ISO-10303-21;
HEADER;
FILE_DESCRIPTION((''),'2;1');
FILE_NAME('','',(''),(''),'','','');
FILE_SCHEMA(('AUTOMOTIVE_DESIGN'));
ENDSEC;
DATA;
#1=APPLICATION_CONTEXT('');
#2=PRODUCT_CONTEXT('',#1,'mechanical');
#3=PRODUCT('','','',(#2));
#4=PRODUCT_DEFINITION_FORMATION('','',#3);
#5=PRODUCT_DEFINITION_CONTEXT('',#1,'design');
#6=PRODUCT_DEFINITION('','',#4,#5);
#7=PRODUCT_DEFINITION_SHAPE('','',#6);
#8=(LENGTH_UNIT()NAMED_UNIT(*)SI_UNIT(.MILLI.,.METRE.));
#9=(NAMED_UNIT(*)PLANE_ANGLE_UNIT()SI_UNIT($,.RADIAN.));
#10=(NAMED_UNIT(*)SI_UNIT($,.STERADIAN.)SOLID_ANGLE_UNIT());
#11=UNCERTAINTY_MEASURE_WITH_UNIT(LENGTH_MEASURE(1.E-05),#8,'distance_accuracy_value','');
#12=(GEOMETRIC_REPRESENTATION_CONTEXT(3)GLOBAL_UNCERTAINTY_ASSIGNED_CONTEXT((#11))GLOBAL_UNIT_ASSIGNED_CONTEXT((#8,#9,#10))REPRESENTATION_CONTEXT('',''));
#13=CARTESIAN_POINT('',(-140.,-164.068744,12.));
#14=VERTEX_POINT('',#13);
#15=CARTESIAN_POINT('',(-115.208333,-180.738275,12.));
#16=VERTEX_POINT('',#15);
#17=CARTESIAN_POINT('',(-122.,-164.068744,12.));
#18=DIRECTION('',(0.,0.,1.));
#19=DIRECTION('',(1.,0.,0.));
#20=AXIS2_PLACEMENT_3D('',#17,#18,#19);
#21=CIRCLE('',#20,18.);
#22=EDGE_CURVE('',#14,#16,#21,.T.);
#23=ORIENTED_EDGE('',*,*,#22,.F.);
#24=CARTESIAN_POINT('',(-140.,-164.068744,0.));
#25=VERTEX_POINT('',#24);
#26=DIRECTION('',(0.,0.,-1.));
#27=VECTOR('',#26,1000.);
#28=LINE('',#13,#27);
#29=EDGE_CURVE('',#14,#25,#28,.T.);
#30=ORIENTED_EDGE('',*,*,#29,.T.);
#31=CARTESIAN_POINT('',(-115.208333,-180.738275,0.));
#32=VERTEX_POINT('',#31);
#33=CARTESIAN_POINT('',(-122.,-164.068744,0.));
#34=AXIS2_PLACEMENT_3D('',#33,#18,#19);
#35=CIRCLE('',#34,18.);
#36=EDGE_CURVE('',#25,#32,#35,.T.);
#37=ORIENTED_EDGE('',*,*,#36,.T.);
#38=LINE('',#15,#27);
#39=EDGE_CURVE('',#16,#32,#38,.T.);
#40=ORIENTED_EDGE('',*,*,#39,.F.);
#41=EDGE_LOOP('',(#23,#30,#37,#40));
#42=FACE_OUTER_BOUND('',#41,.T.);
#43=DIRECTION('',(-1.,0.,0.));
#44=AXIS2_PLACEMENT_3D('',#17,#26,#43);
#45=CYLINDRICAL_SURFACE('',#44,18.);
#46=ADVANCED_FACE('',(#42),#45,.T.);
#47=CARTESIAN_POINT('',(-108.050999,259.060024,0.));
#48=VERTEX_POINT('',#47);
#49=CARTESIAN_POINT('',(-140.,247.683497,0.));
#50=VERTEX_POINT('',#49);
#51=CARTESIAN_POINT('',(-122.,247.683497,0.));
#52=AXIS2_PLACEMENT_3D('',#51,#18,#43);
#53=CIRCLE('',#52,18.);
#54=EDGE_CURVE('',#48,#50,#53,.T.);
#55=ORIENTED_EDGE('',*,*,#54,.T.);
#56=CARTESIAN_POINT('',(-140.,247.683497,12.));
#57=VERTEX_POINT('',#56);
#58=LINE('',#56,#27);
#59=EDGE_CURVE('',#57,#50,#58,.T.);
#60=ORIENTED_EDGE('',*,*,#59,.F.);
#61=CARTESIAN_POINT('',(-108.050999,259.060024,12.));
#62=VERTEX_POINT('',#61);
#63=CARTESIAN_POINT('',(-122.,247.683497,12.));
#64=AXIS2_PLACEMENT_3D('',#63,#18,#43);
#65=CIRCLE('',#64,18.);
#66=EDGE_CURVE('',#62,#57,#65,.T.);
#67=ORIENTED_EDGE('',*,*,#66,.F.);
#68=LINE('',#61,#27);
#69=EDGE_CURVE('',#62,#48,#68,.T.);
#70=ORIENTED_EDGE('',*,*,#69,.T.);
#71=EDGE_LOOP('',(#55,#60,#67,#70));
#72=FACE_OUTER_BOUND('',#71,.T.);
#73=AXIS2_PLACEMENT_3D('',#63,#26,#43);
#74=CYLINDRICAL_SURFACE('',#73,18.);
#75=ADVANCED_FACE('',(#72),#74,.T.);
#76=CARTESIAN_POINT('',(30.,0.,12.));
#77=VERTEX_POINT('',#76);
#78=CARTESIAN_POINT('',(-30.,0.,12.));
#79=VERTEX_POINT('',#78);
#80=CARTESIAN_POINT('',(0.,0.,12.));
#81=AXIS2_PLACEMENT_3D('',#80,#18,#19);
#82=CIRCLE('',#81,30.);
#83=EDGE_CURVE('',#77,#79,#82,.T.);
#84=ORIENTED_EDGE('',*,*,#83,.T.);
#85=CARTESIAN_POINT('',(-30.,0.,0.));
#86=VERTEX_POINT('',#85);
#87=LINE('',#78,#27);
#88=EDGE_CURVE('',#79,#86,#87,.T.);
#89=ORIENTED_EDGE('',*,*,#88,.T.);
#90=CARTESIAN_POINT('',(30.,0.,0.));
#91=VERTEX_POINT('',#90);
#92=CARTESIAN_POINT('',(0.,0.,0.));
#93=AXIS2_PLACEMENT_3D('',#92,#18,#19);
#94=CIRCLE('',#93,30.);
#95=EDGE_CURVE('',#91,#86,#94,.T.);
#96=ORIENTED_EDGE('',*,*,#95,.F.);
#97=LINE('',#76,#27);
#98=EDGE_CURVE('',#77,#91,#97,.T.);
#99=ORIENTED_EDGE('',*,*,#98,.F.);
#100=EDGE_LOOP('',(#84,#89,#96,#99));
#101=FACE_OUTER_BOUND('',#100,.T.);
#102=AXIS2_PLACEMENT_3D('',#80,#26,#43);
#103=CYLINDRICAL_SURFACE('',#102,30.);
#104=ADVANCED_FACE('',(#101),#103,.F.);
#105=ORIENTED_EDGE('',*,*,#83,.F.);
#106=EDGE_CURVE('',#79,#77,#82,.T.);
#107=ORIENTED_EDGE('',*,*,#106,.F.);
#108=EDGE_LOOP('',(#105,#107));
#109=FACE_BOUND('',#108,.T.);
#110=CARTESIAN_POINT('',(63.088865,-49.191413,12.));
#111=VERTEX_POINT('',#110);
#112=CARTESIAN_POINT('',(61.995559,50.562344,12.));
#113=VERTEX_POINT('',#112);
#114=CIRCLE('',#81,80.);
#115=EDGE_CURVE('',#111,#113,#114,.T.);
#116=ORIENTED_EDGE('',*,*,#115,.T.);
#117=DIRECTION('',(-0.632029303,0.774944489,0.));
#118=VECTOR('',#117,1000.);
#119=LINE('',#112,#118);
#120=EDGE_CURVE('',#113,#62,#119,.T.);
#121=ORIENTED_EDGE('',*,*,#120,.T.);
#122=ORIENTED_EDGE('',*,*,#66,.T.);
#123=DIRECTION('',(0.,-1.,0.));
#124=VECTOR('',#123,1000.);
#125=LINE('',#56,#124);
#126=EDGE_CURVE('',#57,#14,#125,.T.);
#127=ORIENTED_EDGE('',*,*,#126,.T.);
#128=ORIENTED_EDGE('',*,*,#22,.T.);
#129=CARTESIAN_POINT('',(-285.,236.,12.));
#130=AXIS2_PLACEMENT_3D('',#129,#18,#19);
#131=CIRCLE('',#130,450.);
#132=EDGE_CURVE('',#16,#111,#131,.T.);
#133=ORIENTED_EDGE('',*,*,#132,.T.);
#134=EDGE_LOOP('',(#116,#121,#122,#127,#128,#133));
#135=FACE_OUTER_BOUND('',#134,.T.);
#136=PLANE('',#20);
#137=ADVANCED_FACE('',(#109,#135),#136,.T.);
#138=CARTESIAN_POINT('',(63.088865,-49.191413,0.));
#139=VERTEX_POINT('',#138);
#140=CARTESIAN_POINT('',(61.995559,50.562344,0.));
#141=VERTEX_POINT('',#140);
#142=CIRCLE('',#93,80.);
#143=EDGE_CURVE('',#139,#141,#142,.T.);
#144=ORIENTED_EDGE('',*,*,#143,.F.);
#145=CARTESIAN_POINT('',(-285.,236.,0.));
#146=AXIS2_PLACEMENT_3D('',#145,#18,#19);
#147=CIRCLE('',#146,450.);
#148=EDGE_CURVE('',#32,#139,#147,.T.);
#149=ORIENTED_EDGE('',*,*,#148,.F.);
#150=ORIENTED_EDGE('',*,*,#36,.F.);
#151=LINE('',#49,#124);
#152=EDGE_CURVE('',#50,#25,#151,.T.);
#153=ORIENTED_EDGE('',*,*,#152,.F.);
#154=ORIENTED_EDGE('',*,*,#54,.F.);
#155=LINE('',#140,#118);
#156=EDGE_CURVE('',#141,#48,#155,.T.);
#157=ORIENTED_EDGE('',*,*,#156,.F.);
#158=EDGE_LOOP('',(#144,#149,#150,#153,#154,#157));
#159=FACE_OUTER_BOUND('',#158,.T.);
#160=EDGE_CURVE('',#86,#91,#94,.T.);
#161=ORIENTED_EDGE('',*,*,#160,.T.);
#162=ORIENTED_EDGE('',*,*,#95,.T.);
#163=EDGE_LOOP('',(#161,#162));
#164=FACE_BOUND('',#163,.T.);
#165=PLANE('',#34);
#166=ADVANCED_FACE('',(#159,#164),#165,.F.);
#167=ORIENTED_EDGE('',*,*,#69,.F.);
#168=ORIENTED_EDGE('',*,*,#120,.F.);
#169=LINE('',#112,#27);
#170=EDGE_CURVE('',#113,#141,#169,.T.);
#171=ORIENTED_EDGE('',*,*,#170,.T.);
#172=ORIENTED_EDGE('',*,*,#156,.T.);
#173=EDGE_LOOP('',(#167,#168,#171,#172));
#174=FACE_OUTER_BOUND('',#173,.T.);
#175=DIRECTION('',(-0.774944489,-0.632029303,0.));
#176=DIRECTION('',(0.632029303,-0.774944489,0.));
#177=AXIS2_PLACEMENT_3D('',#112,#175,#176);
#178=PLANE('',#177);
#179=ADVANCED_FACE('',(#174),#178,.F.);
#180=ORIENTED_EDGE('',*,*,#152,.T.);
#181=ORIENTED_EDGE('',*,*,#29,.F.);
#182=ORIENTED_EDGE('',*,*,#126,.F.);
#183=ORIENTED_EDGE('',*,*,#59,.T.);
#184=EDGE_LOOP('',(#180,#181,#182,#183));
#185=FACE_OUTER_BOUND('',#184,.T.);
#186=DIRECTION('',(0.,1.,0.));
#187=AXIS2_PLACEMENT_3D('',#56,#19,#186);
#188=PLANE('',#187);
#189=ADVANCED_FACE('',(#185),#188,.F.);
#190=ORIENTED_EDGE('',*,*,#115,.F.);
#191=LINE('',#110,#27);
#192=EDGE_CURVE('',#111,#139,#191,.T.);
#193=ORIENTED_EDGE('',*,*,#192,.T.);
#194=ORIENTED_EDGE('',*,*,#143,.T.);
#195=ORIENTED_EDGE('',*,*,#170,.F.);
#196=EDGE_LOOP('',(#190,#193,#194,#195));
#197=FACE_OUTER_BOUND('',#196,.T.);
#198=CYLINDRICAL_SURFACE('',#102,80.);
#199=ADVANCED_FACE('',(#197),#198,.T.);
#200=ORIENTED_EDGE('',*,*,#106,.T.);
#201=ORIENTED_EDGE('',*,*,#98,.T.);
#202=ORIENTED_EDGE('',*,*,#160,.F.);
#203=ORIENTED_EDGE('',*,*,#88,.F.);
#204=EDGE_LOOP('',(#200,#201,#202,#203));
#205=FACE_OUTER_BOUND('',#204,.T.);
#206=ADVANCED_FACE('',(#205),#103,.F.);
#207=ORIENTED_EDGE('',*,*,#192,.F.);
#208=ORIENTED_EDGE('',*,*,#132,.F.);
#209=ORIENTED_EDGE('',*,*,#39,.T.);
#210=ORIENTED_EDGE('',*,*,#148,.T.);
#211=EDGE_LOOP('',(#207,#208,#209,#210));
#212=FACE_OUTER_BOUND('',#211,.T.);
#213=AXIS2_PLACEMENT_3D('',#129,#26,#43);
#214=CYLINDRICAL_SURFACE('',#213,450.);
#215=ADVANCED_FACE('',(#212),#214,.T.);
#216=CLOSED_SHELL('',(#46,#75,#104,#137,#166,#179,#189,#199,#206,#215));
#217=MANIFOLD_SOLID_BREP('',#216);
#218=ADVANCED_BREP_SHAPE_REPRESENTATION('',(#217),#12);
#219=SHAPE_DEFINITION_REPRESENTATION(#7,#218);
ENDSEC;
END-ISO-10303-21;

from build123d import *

# Parameters (mm, degrees)
SKETCH1_R           = 30
BOSS_EXTRUDE1_DEPTH = 12


with BuildPart() as part:
    # Sketch1 → Boss-Extrude1 (new body)
    with BuildSketch(Plane.XY):
        with BuildLine():
            Line((-140, 247.683496575), (-140, -164.068744093))
            ThreePointArc((-140, -164.068744093), (-132.043654713, -179.006113339), (-115.208333333, -180.738275097))
            ThreePointArc((-115.208333333, -180.738275097), (-17.836743976, -126.110196806), (63.088864614, -49.191413496))
            ThreePointArc((63.088864614, -49.191413496), (79.995195531, 0.876750818), (61.995559096, 50.562344213))
            Line((61.995559096, 50.562344213), (-108.050999203, 259.060024023))
            ThreePointArc((-108.050999203, 259.060024023), (-128.038128256, 264.640530725), (-140, 247.683496575))
        make_face()
        Circle(SKETCH1_R, mode=Mode.SUBTRACT)
    extrude(amount=BOSS_EXTRUDE1_DEPTH)


solid = part.part
